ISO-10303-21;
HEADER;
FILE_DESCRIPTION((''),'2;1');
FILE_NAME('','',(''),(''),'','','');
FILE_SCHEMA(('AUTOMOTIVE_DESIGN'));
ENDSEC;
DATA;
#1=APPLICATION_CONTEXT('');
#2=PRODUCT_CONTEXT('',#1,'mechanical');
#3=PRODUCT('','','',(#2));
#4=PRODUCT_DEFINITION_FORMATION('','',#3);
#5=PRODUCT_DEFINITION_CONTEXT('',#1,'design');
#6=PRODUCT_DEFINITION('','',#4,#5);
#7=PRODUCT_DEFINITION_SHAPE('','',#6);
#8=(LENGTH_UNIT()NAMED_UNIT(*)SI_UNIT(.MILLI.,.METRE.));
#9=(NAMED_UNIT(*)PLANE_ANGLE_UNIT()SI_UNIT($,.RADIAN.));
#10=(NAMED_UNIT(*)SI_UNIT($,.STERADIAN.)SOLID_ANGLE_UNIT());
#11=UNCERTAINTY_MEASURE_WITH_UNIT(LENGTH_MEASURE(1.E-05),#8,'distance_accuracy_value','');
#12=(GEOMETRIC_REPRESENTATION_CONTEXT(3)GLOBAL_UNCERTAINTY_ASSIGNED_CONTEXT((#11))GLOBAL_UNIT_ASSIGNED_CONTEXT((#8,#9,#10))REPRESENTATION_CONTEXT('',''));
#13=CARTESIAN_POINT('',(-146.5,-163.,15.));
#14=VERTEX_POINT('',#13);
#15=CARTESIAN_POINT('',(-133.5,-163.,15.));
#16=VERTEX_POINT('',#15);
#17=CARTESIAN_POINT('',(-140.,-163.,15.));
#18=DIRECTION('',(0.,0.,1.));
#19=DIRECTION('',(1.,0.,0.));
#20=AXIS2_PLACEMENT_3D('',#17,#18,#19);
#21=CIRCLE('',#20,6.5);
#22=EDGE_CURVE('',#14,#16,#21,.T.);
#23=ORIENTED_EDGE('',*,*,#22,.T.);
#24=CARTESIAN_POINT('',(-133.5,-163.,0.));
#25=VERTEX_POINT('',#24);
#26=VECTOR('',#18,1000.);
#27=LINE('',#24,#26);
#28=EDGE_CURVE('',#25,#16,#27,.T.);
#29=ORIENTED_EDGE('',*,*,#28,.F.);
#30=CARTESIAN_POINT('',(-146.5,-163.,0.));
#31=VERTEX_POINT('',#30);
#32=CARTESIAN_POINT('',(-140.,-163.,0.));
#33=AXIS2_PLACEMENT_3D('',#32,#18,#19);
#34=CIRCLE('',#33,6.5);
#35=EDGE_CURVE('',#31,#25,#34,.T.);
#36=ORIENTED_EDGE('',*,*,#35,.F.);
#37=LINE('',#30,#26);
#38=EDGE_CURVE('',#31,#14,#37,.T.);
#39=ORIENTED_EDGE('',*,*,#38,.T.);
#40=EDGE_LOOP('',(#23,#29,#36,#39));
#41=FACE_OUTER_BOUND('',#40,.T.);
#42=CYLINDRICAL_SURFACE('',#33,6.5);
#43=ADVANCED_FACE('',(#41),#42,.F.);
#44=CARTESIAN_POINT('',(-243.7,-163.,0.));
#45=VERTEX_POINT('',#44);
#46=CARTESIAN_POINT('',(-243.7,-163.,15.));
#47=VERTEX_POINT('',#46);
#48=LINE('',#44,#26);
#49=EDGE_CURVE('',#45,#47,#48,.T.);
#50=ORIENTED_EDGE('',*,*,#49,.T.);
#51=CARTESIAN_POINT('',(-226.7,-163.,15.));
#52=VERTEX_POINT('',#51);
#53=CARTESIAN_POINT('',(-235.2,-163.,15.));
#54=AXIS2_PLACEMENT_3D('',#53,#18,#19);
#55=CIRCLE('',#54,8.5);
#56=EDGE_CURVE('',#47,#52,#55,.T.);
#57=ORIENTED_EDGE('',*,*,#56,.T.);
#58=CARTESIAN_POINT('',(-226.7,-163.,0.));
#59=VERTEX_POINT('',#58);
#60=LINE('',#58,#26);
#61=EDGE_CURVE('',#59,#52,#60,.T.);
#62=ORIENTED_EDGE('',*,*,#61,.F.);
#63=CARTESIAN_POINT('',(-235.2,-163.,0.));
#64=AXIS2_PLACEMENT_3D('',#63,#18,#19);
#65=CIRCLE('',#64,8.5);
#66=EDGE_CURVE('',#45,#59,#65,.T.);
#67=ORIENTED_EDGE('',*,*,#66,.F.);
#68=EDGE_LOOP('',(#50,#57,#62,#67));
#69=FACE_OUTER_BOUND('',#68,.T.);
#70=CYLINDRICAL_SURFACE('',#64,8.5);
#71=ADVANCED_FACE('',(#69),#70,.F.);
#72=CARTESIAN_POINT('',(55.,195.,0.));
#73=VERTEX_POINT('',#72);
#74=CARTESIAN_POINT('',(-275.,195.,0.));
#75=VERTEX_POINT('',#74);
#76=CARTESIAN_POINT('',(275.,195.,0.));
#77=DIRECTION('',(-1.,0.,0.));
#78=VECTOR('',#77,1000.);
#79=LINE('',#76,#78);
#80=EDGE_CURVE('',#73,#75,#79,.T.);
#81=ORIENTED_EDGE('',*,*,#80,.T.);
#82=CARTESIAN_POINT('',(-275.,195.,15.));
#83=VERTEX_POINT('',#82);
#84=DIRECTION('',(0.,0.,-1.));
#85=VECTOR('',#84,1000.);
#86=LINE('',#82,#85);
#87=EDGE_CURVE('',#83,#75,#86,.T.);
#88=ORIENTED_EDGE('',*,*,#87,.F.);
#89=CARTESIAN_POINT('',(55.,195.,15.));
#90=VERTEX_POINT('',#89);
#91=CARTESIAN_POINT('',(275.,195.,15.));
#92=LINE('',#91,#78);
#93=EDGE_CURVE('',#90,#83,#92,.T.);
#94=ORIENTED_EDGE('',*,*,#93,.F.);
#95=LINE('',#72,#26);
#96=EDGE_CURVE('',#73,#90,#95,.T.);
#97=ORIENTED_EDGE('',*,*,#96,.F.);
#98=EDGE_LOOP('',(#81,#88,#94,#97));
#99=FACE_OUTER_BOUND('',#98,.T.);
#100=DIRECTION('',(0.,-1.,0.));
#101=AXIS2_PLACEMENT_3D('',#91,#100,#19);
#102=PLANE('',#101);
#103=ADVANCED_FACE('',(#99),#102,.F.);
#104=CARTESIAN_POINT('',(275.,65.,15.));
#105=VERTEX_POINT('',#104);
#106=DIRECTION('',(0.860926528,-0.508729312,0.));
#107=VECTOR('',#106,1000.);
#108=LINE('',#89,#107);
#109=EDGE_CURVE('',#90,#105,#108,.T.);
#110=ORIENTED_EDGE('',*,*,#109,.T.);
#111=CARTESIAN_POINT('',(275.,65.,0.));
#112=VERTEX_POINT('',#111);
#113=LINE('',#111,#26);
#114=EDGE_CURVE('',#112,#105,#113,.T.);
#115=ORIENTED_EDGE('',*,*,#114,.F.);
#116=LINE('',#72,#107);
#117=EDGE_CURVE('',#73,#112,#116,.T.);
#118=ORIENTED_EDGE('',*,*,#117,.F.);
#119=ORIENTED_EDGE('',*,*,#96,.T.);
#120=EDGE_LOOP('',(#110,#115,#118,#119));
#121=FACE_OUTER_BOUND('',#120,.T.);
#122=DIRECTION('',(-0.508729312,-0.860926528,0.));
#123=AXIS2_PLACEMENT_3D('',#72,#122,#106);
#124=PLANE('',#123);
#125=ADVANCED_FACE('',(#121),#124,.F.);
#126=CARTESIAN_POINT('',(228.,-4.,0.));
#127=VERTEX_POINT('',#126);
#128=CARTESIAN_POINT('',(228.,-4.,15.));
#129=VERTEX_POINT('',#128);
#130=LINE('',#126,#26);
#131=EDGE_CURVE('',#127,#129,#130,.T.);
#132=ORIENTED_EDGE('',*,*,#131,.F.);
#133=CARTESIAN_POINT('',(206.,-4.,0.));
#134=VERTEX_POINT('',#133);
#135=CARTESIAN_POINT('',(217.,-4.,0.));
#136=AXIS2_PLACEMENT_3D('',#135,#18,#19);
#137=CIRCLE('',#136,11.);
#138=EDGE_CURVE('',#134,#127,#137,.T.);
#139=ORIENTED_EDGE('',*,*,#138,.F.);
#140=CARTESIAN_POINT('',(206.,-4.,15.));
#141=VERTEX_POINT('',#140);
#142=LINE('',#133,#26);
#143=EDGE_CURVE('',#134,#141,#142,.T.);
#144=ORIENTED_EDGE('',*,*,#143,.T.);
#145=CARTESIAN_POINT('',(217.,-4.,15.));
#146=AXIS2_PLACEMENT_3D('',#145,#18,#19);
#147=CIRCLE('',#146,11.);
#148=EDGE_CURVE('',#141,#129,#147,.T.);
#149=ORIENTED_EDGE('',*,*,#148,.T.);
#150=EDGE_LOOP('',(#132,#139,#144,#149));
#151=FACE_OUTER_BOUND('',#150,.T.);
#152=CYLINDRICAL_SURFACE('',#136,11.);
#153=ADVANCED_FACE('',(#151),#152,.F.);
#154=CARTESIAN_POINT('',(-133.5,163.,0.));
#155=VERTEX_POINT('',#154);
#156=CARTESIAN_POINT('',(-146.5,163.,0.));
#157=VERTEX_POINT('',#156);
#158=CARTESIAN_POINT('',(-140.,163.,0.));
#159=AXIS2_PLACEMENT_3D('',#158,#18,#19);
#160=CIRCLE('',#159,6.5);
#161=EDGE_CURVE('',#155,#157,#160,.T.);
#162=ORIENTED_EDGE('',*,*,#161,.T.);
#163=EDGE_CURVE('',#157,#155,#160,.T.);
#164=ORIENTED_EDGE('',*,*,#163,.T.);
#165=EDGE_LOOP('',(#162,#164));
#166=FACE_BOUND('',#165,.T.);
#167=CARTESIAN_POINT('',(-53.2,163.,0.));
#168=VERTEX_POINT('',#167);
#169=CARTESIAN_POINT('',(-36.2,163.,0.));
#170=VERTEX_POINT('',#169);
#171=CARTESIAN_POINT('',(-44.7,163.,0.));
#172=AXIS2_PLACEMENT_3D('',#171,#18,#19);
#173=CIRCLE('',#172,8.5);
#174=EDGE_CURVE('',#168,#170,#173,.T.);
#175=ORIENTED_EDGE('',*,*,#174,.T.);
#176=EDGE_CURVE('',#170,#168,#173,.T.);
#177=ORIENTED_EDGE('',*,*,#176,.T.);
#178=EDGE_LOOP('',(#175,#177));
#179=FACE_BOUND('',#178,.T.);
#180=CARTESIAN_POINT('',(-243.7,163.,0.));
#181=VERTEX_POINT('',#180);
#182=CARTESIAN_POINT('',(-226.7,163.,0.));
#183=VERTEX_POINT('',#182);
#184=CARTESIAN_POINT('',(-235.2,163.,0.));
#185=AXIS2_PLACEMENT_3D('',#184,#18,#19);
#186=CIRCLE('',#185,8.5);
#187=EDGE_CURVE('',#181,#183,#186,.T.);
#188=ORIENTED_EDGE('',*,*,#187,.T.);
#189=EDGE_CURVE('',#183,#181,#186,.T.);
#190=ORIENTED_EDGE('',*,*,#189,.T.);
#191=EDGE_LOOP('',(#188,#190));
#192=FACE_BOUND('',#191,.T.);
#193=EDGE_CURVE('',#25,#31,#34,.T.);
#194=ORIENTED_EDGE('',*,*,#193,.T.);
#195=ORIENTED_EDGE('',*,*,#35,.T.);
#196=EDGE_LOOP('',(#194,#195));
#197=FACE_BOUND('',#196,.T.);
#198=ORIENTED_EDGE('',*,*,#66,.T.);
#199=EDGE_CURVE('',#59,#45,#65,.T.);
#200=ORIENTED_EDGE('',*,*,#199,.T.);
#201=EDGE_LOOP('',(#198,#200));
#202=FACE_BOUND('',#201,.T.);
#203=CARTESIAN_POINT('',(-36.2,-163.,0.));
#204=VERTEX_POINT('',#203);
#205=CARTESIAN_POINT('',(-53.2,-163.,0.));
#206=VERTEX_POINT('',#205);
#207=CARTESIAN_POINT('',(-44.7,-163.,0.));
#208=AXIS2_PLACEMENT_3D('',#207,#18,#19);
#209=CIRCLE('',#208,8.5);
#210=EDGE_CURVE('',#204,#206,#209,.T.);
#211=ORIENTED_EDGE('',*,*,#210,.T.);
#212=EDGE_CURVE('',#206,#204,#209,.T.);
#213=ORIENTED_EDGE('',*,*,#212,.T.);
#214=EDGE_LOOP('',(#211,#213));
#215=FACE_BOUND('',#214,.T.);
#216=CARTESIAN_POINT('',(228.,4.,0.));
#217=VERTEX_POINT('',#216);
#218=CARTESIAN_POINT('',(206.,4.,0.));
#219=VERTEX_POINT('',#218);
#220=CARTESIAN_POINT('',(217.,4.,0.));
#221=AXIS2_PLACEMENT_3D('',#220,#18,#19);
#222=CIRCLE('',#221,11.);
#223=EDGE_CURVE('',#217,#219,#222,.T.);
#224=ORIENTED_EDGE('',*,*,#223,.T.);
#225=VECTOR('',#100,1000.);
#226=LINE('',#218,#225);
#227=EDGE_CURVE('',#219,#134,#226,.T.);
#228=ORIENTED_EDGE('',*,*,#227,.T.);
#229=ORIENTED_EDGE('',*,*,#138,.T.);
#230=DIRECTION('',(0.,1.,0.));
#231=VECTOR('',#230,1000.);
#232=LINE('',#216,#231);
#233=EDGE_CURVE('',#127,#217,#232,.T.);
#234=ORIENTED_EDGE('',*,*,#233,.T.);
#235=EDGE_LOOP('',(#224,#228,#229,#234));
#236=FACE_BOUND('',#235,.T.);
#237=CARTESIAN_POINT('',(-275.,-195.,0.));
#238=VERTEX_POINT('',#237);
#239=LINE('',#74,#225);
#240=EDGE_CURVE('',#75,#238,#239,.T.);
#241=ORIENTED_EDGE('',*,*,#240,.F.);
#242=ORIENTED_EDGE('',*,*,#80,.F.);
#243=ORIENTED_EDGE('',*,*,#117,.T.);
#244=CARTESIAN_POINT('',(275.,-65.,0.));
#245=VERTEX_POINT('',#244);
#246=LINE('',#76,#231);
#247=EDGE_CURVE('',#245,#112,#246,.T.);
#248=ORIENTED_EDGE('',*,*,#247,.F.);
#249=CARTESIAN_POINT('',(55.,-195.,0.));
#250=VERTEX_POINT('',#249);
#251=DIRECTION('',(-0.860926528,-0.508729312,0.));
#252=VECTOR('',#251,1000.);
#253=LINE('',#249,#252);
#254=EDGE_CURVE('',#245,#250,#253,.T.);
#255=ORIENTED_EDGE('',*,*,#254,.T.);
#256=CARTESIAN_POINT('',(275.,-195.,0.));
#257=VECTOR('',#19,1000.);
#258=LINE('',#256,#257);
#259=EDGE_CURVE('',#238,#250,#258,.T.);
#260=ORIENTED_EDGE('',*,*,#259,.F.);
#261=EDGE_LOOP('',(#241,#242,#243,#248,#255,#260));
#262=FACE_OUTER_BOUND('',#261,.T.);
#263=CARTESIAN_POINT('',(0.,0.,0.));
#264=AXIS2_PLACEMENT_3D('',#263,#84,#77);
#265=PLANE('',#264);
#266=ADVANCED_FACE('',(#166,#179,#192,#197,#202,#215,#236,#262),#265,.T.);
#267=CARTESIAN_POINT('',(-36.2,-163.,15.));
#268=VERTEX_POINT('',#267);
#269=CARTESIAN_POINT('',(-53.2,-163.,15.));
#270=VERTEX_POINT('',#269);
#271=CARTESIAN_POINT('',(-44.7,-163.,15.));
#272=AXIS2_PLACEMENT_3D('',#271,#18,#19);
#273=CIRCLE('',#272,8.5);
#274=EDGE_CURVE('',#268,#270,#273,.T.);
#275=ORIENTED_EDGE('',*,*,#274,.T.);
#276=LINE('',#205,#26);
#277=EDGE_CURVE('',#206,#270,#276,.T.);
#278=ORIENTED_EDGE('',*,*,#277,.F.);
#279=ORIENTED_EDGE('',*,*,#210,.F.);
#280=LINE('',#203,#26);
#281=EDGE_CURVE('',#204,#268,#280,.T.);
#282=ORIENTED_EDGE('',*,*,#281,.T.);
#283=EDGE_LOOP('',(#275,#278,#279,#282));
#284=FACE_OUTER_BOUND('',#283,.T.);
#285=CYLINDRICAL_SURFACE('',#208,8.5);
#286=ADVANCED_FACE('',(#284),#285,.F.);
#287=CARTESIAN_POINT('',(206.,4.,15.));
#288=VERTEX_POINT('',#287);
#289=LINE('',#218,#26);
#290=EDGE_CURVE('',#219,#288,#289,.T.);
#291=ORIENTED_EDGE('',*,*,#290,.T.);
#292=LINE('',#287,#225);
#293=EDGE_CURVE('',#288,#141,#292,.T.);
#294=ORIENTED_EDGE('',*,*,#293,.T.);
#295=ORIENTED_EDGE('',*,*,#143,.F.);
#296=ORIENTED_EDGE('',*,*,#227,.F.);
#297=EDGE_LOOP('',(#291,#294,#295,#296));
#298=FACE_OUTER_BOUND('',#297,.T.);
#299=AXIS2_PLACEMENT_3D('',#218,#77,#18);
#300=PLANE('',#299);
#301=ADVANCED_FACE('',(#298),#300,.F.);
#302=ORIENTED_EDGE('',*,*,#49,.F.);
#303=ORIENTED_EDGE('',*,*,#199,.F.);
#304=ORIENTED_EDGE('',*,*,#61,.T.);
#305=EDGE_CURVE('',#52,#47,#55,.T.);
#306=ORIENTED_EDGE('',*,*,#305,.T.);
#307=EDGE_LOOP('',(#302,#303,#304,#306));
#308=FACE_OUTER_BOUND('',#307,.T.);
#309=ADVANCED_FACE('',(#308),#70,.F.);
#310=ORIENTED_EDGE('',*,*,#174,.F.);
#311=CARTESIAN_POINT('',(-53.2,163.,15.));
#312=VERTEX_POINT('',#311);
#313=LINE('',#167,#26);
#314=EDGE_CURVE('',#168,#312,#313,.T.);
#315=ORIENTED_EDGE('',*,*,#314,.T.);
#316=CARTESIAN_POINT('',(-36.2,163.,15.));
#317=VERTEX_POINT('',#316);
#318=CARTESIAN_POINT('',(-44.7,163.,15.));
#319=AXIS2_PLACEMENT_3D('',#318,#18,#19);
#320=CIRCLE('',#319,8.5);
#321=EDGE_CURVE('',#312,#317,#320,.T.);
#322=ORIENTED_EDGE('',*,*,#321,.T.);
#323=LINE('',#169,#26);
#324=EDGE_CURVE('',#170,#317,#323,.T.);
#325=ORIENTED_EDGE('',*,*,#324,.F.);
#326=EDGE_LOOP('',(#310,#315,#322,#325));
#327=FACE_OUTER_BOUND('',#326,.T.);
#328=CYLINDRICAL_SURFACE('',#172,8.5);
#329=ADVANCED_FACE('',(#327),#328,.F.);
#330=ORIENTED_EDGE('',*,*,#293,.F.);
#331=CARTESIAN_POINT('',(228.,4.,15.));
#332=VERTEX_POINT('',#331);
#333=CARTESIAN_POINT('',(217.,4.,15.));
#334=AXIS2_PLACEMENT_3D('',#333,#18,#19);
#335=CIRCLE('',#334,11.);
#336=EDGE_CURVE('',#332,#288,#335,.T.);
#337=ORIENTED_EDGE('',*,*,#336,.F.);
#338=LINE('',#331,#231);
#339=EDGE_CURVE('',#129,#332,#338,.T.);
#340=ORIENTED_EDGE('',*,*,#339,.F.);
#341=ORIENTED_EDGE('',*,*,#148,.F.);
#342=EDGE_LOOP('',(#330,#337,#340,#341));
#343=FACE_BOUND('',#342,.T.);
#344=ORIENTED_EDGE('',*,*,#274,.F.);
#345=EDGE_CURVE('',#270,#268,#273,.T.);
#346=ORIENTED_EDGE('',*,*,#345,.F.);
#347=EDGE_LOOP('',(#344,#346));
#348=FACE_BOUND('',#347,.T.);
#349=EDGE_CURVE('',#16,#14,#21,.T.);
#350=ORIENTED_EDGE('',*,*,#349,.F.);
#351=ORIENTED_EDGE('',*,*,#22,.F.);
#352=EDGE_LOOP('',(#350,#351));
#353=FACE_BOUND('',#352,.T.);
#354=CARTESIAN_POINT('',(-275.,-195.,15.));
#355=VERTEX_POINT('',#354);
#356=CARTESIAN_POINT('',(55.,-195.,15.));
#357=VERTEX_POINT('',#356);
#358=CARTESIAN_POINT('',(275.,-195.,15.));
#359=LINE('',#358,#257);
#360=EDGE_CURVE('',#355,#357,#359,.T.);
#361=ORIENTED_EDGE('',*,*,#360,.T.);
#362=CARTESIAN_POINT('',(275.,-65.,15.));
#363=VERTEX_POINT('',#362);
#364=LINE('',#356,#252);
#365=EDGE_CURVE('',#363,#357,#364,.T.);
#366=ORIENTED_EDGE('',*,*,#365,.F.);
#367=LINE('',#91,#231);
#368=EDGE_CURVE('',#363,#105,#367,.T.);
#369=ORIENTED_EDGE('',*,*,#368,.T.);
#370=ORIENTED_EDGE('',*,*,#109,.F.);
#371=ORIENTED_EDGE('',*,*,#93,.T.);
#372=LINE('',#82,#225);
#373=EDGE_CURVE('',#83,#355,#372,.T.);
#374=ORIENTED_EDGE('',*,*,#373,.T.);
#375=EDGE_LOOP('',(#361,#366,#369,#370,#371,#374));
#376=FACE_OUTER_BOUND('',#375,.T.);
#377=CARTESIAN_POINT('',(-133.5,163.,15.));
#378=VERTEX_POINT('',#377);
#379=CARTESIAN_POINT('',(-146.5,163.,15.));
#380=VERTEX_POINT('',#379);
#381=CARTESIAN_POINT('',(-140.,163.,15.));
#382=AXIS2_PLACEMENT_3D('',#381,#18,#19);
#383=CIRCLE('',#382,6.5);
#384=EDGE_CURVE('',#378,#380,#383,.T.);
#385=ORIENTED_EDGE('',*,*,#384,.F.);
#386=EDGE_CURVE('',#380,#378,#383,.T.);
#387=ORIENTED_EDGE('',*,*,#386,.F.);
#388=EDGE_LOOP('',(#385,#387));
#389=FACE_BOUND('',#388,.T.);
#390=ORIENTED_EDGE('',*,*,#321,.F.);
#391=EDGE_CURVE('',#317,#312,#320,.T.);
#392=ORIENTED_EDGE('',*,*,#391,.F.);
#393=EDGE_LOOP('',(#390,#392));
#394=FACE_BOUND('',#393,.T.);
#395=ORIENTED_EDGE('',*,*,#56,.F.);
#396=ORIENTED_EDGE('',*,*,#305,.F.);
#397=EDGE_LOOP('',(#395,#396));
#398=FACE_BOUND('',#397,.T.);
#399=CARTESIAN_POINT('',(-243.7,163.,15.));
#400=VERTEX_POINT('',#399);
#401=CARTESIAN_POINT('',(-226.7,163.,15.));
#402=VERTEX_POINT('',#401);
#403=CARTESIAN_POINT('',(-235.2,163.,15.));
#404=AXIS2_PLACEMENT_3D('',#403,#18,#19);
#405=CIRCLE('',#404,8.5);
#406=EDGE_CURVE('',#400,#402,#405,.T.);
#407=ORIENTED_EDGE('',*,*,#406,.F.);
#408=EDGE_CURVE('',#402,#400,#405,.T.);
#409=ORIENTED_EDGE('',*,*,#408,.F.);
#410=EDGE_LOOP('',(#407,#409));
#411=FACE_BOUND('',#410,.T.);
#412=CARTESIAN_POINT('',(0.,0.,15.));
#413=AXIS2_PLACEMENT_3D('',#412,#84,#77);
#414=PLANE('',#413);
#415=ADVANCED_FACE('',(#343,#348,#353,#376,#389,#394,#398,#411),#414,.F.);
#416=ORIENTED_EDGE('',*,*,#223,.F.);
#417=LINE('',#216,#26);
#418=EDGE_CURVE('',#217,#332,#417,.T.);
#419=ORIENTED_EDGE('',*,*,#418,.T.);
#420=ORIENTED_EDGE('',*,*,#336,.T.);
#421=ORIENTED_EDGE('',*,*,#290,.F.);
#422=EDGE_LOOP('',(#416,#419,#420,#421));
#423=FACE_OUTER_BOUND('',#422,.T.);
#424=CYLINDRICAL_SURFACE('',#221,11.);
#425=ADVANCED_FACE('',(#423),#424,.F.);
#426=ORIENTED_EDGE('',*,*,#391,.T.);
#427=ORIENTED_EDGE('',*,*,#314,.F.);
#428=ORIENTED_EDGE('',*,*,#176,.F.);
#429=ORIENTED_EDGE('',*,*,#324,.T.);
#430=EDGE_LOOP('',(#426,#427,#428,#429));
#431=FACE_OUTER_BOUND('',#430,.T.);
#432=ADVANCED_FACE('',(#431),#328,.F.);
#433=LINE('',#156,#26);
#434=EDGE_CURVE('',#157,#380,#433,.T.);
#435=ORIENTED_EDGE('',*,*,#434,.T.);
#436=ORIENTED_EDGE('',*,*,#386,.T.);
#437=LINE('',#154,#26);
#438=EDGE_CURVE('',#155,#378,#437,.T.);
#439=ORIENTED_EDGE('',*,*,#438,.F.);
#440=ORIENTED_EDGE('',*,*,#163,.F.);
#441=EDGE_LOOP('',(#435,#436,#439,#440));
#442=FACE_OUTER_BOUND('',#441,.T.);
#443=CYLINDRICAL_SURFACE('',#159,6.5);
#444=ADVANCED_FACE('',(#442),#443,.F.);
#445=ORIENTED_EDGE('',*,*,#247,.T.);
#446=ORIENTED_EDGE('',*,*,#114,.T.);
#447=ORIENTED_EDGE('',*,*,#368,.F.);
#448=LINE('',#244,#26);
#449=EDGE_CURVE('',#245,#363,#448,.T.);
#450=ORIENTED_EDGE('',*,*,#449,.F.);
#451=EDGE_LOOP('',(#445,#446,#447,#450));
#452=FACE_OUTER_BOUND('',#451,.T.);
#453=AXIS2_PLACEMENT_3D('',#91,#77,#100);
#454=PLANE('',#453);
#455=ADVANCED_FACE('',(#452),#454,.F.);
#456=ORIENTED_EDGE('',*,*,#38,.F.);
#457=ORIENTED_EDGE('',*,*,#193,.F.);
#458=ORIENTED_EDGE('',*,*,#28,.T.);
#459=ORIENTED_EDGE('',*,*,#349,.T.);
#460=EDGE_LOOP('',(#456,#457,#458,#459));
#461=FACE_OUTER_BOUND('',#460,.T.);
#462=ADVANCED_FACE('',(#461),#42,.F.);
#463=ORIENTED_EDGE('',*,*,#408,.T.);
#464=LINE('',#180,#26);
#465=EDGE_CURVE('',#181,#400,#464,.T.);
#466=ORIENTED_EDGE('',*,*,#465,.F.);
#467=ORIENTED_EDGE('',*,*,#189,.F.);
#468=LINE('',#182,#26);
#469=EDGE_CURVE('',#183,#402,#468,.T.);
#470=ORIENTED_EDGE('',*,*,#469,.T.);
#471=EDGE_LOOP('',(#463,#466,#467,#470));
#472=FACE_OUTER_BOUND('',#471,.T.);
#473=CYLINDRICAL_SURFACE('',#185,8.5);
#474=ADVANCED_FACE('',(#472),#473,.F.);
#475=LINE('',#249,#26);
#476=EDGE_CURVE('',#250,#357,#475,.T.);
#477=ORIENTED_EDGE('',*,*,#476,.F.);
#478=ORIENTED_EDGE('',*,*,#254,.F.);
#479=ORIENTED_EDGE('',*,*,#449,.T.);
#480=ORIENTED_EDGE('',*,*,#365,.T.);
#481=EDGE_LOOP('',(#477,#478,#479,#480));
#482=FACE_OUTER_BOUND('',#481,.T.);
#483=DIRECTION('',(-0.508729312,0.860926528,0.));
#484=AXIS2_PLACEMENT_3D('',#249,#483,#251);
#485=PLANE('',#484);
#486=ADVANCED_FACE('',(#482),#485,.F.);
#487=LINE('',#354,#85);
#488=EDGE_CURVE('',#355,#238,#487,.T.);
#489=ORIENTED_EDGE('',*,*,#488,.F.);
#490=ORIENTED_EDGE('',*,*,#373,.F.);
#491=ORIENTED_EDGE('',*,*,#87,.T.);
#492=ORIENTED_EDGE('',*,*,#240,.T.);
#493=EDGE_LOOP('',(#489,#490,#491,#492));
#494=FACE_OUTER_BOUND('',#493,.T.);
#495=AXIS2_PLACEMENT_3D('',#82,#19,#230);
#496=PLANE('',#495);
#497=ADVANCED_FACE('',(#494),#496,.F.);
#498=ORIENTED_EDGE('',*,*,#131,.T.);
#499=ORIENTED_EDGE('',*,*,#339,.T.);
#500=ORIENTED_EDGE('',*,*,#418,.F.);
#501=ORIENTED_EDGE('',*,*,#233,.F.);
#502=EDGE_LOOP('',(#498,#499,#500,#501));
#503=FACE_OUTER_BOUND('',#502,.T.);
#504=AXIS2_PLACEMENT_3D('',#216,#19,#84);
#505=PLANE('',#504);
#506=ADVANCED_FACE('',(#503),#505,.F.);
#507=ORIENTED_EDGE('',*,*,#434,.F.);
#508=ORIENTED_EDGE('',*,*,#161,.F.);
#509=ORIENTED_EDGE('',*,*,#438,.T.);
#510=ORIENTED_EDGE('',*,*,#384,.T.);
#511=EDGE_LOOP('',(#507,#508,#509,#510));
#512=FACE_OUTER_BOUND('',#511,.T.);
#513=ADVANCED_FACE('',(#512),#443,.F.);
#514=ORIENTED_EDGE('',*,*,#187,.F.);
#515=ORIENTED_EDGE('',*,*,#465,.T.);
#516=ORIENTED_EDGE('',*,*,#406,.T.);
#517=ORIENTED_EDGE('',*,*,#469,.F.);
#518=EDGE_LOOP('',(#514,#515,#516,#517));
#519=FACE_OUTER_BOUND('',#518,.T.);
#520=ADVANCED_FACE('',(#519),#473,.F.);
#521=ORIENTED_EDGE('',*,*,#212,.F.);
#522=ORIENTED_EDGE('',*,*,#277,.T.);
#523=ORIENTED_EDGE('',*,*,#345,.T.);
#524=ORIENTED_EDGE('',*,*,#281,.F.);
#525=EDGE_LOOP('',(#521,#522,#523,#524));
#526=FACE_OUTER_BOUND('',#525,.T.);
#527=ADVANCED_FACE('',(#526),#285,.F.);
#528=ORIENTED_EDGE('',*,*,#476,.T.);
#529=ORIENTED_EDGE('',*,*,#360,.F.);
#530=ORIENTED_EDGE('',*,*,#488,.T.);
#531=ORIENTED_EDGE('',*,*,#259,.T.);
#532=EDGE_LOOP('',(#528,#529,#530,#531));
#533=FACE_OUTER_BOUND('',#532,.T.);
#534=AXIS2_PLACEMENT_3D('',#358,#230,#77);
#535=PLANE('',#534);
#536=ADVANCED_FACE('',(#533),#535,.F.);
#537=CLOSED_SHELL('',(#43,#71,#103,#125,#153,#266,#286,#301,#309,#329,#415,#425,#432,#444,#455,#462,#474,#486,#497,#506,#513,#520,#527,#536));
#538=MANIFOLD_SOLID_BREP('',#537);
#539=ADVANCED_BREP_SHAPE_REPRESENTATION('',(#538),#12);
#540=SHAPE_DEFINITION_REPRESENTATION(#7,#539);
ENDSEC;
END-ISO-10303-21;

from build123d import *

# Parameters (mm, degrees)
SKETCH_1_W          = 550
SKETCH_1_H          = 390
EXTRUDE_1_DEPTH     = 15
SKETCH_2_R          = 8.5
SKETCH_2_R_2        = 6.5
CUT_EXTRUDE_1_DEPTH = 15


with BuildPart() as part:
    # 草图1 → 凸台-拉伸1 (new body)
    with BuildSketch(Plane.XY):
        Rectangle(SKETCH_1_W, SKETCH_1_H)
    extrude(amount=EXTRUDE_1_DEPTH)

    # 草图2 → 切除-拉伸1 (cut)
    with BuildSketch(Plane.XY.offset(15)):
        with Locations((-235.2, 163)):
            Circle(SKETCH_2_R)
        with Locations((-235.2, -163)):
            Circle(SKETCH_2_R)
        with Locations((-140, -163)):
            Circle(SKETCH_2_R_2)
        with Locations((-44.7, -163)):
            Circle(SKETCH_2_R)
        with Locations((-140, 163)):
            Circle(SKETCH_2_R_2)
        with Locations((-44.7, 163)):
            Circle(SKETCH_2_R)
        Polygon((55, 195), (275, 65), (275, 195), align=None)
        Polygon((55, -195), (275, -65), (275, -195), align=None)
        with BuildLine():
            Line((228, 4), (228, -4))
            ThreePointArc((228, -4), (217, -15), (206, -4))
            Line((206, -4), (206, 4))
            ThreePointArc((206, 4), (217, 15), (228, 4))
        make_face()
    extrude(amount=-CUT_EXTRUDE_1_DEPTH, mode=Mode.SUBTRACT)


solid = part.part
